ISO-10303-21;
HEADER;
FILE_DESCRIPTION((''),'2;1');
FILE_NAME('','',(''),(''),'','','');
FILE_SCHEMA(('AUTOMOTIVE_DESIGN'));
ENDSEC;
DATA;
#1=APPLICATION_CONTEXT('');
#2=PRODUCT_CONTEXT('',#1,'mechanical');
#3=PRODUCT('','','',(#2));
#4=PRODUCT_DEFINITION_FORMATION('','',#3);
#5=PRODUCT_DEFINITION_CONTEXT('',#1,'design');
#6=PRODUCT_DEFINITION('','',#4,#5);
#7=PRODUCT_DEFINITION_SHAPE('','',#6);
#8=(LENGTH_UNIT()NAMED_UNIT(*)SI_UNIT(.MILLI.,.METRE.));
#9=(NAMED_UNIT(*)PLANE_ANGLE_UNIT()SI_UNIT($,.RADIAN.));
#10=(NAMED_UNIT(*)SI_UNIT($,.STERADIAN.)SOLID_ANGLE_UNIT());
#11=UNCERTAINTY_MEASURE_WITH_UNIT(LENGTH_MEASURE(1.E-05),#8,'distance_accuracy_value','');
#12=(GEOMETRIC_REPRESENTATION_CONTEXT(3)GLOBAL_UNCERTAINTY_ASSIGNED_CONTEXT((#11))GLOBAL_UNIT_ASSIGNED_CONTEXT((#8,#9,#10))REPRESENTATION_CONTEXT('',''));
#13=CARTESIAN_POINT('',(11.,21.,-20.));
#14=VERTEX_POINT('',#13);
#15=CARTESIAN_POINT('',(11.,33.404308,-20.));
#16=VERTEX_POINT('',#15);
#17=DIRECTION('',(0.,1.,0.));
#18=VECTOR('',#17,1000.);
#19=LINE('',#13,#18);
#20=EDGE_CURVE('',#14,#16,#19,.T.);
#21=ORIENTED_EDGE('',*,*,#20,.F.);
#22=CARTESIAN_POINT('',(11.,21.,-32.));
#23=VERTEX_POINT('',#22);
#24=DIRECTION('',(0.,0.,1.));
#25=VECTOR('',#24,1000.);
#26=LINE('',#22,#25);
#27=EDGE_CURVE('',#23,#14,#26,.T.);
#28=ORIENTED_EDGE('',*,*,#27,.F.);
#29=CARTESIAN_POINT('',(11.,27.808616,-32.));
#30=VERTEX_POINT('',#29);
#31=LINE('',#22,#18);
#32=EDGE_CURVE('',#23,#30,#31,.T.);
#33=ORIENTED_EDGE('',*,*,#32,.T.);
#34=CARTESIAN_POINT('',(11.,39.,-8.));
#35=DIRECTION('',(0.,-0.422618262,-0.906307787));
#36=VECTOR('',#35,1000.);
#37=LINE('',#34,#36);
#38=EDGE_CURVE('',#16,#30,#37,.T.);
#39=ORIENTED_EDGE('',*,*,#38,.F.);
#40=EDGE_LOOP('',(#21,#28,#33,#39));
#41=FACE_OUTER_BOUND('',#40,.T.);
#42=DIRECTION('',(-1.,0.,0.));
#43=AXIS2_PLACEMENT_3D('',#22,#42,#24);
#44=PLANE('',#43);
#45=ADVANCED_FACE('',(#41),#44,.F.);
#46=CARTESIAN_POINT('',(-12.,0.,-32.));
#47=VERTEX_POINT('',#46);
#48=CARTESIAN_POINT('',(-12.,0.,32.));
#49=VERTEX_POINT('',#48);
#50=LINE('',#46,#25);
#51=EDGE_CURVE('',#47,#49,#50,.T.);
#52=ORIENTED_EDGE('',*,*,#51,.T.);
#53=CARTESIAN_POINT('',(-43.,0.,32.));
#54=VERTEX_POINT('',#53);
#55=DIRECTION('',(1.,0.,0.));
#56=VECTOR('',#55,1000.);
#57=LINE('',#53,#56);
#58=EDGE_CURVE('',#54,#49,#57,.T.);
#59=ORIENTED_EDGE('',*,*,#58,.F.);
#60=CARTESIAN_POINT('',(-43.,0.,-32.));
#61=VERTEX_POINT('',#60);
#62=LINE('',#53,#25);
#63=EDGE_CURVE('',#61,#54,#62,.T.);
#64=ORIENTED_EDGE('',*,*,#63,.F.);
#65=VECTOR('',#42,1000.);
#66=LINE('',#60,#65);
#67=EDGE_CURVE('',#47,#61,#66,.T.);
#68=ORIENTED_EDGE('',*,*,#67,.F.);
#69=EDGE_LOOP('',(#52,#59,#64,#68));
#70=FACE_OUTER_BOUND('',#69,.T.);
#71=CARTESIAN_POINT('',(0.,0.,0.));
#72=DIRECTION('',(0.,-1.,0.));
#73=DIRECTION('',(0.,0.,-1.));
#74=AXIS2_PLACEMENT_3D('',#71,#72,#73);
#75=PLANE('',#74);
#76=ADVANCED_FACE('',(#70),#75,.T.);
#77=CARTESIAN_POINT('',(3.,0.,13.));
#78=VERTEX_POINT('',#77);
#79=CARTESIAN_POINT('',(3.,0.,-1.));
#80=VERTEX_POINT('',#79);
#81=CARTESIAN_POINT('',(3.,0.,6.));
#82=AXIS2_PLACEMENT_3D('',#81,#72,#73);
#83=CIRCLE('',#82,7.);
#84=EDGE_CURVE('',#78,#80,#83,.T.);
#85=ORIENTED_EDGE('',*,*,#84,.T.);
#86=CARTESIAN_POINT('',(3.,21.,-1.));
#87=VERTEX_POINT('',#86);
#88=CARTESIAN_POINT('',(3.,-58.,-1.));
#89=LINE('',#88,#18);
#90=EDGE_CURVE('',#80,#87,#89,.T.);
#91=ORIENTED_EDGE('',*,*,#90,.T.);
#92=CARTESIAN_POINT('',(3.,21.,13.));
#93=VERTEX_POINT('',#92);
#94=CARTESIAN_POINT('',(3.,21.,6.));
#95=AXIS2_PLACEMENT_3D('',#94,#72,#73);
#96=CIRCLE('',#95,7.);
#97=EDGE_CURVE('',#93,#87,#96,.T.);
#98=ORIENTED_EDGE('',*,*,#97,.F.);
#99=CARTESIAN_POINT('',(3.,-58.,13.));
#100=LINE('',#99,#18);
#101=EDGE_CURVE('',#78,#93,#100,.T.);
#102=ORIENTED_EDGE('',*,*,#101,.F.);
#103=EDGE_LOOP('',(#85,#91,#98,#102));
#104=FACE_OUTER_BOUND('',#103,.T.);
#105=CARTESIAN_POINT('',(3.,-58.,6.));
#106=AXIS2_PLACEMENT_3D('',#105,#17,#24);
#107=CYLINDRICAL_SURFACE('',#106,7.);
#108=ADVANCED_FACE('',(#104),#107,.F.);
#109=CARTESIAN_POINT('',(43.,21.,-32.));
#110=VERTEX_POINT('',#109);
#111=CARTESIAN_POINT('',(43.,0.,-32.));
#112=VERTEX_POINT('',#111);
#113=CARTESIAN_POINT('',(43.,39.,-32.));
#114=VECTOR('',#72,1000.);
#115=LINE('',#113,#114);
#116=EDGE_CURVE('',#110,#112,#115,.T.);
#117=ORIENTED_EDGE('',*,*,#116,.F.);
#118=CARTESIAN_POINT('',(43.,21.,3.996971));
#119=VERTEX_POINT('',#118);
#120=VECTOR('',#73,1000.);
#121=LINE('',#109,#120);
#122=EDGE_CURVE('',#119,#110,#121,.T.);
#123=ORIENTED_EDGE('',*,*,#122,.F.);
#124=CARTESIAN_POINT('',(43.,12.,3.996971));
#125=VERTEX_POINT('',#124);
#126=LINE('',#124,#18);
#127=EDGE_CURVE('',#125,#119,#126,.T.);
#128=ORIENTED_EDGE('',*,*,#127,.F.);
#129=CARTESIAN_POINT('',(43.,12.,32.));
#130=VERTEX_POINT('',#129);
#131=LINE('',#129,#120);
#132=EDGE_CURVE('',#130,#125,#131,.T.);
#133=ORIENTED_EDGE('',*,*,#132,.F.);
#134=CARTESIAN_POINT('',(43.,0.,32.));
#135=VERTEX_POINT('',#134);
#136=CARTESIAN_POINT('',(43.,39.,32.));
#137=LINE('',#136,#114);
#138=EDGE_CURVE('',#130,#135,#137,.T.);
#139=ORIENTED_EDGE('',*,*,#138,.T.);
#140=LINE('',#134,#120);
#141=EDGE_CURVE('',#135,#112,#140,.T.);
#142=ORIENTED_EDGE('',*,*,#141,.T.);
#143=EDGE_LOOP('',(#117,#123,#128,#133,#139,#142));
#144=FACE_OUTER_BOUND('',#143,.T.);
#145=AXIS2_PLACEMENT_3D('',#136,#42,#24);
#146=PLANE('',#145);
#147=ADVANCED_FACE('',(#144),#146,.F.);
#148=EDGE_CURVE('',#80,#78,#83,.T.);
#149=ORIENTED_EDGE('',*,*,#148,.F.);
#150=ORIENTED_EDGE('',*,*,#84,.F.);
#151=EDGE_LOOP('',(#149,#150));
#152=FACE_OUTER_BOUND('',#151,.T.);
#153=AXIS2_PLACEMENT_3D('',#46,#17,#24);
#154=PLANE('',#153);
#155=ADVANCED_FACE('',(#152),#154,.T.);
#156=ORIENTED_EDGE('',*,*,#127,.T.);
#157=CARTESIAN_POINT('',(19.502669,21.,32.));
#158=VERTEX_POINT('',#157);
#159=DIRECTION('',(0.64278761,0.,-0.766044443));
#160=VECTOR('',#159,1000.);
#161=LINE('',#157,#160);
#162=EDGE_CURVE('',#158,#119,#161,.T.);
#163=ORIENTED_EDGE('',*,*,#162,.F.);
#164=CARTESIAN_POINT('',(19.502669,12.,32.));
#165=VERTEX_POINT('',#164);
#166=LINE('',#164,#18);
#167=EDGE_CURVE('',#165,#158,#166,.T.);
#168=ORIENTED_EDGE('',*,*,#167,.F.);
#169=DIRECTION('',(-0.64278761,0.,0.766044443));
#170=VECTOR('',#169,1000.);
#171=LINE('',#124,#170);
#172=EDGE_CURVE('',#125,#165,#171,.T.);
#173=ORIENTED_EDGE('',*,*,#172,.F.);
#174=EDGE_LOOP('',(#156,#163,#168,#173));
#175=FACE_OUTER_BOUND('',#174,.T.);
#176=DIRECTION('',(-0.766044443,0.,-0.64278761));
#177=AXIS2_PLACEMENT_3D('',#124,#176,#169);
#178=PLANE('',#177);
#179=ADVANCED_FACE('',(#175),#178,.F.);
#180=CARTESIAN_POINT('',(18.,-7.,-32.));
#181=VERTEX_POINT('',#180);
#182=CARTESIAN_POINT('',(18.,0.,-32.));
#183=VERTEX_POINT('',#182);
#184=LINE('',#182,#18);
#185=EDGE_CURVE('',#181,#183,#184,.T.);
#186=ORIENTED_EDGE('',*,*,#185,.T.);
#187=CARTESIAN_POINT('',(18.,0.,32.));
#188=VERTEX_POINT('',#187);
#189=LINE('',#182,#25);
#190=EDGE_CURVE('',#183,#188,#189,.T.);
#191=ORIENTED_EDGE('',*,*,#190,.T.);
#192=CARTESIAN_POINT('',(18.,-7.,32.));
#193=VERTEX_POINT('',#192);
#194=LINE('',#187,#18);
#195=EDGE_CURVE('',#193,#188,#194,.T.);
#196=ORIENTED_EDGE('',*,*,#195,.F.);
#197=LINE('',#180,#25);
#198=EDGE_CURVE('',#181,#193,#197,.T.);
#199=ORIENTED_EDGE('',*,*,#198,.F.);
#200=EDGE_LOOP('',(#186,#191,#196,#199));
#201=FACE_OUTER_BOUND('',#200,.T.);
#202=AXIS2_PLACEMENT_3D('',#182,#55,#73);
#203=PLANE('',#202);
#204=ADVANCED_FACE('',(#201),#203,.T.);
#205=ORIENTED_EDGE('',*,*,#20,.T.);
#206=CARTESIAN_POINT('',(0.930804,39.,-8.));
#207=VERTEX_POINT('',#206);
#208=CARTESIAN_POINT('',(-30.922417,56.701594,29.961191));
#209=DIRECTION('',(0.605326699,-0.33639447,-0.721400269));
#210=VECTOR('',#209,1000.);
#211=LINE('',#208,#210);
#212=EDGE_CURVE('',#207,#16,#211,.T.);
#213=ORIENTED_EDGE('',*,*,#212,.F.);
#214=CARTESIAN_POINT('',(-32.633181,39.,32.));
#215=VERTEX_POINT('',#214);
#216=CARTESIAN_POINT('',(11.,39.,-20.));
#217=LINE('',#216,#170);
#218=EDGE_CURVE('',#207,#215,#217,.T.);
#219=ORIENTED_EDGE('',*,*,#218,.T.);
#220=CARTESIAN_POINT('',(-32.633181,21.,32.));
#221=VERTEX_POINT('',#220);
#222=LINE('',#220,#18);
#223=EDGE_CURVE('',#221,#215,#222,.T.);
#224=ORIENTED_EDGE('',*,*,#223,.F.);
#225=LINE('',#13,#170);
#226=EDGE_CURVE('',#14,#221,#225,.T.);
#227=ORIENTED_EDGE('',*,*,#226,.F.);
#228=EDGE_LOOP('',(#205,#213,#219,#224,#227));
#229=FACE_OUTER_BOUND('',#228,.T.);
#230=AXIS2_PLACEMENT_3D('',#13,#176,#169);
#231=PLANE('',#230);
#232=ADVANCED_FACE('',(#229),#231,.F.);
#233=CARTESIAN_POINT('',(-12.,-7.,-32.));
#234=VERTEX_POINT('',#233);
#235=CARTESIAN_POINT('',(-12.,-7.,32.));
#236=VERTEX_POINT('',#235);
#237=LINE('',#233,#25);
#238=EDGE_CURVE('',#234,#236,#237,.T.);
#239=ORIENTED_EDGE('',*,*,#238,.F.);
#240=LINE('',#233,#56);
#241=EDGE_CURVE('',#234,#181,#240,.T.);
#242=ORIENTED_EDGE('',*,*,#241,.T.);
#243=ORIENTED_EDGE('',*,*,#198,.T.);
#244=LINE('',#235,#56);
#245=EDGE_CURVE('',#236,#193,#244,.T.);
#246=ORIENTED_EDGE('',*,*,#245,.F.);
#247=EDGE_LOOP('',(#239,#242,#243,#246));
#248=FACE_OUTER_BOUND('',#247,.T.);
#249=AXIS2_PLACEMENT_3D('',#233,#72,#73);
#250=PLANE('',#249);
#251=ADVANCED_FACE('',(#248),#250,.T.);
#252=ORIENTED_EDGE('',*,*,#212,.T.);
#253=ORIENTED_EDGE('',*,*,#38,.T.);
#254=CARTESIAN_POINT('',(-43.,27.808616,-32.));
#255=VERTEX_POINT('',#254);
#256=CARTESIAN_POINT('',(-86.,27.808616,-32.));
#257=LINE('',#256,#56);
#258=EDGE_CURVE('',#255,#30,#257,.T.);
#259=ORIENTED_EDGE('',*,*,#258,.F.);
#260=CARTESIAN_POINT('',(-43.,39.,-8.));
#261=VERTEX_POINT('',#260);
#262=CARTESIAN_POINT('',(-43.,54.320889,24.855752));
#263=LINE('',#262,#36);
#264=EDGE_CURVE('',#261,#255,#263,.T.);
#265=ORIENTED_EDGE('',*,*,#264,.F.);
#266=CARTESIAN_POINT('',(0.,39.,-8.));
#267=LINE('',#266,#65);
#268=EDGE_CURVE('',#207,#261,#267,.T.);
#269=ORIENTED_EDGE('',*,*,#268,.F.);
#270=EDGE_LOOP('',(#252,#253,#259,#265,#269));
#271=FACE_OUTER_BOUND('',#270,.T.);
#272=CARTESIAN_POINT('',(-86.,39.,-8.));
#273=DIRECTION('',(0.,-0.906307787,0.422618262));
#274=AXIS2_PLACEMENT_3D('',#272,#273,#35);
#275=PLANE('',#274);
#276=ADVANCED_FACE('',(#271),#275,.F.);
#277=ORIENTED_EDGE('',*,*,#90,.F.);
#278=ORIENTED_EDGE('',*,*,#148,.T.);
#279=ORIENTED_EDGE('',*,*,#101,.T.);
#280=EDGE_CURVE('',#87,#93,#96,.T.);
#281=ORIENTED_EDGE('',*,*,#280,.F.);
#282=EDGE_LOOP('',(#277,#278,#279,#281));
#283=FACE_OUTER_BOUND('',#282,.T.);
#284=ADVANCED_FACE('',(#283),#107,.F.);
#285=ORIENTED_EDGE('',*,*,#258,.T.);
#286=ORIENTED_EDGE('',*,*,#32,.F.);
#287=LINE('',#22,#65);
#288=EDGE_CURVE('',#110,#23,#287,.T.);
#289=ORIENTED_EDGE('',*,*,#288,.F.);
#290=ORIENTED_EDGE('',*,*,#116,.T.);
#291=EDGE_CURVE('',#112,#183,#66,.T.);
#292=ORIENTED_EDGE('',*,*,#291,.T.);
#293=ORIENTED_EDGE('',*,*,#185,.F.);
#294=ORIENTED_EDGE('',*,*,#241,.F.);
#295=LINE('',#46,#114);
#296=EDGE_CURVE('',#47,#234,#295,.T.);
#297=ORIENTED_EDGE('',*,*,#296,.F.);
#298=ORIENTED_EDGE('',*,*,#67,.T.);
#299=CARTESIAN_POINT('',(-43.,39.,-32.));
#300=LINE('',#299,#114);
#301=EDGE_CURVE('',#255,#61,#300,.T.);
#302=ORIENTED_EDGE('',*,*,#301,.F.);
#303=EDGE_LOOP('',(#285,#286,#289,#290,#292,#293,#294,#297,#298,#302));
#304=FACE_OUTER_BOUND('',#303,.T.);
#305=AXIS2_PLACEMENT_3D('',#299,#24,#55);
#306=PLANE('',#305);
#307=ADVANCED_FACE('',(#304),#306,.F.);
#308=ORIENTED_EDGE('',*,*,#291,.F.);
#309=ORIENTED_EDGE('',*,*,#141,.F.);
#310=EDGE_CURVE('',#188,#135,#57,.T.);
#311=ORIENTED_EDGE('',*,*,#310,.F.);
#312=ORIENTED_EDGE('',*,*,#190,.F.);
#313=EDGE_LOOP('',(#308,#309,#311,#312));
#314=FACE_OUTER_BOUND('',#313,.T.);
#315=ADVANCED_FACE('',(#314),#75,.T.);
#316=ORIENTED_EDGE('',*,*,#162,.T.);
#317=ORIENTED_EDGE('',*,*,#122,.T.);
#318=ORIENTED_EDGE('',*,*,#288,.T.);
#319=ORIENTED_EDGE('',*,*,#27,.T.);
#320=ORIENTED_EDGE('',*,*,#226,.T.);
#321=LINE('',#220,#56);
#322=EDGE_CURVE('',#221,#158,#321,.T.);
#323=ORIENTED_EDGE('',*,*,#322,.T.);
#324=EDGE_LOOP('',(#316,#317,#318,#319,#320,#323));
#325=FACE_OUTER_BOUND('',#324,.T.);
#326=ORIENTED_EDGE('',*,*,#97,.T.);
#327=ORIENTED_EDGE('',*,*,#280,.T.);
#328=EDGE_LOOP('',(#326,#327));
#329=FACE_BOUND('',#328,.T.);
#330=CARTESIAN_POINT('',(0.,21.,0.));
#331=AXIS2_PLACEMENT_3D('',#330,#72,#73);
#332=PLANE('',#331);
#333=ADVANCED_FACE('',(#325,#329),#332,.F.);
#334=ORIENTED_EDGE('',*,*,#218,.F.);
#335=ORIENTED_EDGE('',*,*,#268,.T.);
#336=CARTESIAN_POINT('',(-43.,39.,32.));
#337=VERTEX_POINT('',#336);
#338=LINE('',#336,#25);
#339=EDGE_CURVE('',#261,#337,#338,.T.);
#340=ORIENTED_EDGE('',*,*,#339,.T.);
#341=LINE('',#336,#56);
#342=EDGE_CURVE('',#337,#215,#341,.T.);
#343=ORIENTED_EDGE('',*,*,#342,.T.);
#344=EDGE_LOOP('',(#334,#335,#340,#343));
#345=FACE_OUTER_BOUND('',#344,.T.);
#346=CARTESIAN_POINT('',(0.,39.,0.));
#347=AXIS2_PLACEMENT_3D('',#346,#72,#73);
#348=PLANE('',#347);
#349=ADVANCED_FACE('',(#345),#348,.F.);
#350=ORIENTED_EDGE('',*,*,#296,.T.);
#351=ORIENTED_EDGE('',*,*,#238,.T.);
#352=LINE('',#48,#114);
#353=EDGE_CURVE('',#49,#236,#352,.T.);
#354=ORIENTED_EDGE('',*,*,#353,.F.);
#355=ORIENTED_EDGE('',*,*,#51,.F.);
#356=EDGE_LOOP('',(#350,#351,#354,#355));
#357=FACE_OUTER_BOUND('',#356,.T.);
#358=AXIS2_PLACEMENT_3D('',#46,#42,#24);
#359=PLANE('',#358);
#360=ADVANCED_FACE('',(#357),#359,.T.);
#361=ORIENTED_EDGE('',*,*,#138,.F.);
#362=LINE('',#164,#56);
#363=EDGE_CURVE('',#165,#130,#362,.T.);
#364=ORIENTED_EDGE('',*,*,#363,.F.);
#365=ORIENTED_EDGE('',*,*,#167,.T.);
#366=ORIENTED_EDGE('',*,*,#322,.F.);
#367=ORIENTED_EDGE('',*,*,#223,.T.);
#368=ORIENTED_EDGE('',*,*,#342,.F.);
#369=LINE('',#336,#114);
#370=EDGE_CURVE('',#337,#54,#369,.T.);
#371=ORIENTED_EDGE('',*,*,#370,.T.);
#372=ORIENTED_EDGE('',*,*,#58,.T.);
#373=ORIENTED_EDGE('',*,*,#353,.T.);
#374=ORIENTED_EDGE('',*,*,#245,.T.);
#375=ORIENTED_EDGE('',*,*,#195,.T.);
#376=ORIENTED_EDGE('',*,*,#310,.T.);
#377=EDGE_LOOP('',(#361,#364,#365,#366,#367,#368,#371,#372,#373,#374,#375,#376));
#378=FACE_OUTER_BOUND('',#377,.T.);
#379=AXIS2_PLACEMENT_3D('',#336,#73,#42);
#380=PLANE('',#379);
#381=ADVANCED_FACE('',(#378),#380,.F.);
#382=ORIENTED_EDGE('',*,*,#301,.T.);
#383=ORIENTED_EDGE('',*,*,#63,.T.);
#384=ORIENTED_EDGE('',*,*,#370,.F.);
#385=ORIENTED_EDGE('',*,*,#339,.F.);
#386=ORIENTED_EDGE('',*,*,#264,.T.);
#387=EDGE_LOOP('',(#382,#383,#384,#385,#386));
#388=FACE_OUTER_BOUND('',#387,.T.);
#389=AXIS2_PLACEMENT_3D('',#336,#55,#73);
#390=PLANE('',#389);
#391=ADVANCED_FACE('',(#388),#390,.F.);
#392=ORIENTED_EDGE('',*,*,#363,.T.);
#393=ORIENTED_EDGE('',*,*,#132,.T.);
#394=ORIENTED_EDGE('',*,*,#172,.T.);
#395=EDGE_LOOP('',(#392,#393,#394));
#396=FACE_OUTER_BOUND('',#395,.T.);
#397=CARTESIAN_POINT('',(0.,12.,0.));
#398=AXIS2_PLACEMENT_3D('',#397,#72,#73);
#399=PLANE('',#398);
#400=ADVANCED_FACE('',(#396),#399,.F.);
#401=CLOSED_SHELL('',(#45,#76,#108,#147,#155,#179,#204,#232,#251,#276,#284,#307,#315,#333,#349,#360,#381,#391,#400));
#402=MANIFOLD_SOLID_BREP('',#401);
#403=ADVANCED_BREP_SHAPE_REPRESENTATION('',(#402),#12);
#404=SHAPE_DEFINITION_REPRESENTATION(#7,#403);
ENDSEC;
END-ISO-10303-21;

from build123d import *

# Parameters (mm, degrees)
BASE_BLOCK_SKETCH_W         = 86
BASE_BLOCK_SKETCH_H         = 64
BASE_BLOCK_86X64X39_DEPTH   = 39
ANGLED_SIDE_CUT_25DEG_DEPTH = 129
TOP_STEP_CUT_SKETCH_R       = 7
TOP_STEP_CUT_DEPTH          = 18
CORNER_BEVEL_CUT_DEPTH      = 27
THROUGH_HOLE_SKETCH_R       = 7
THROUGH_HOLE_DEPTH          = 97
GUIDE_TONGUE_SKETCH_W       = 30
GUIDE_TONGUE_SKETCH_H       = 7
GUIDE_TONGUE_DEPTH          = 64


with BuildPart() as part:
    # Base Block Sketch → Base Block 86x64x39 (new body)
    with BuildSketch(Plane(origin=(0, 0, 0), x_dir=(1, 0, 0), z_dir=(0, 1, 0))):
        Rectangle(BASE_BLOCK_SKETCH_W, BASE_BLOCK_SKETCH_H)
    extrude(amount=BASE_BLOCK_86X64X39_DEPTH)

    # Angled Side Cut Sketch → Angled Side Cut 25deg (cut)
    with BuildSketch(Plane(origin=(43, 0, 0), x_dir=(0, 0, -1), z_dir=(1, 0, 0))):
        Polygon((8, 39), (32, 27.808616204), (32, 39), align=None)
    extrude(amount=-ANGLED_SIDE_CUT_25DEG_DEPTH, mode=Mode.SUBTRACT)

    # Top Step Cut Sketch → Top Step Cut (cut)
    with BuildSketch(Plane(origin=(0, 39, 0), x_dir=(1, 0, 0), z_dir=(0, 1, 0))):
        Polygon((11, 32), (11, 20), (-32.633180821, -32), (19.502668792, -32), (43, -3.996971117), (43, 32), align=None)
        with Locations(Location((3, -6, 0), (0, 0, 270))):
            Circle(TOP_STEP_CUT_SKETCH_R, mode=Mode.SUBTRACT)
    extrude(amount=-TOP_STEP_CUT_DEPTH, mode=Mode.SUBTRACT)

    # Corner Bevel Cut Sketch → Corner Bevel Cut (cut)
    with BuildSketch(Plane(origin=(0, 39, 0), x_dir=(1, 0, 0), z_dir=(0, 1, 0))):
        Polygon((43, -3.996971117), (19.502668792, -32), (43, -32), align=None)
    extrude(amount=-CORNER_BEVEL_CUT_DEPTH, mode=Mode.SUBTRACT)

    # Through Hole Sketch → Through Hole (cut)
    with BuildSketch(Plane(origin=(0, 39, 0), x_dir=(1, 0, 0), z_dir=(0, 1, 0))):
        with Locations(Location((3, -6, 0), (0, 0, 90))):
            Circle(THROUGH_HOLE_SKETCH_R)
    extrude(amount=-THROUGH_HOLE_DEPTH, mode=Mode.SUBTRACT)

    # Guide Tongue Sketch → Guide Tongue (add)
    with BuildSketch(Plane.XY.offset(32)):
        with Locations((3, -3.5)):
            Rectangle(GUIDE_TONGUE_SKETCH_W, GUIDE_TONGUE_SKETCH_H)
    extrude(amount=-GUIDE_TONGUE_DEPTH)


solid = part.part
